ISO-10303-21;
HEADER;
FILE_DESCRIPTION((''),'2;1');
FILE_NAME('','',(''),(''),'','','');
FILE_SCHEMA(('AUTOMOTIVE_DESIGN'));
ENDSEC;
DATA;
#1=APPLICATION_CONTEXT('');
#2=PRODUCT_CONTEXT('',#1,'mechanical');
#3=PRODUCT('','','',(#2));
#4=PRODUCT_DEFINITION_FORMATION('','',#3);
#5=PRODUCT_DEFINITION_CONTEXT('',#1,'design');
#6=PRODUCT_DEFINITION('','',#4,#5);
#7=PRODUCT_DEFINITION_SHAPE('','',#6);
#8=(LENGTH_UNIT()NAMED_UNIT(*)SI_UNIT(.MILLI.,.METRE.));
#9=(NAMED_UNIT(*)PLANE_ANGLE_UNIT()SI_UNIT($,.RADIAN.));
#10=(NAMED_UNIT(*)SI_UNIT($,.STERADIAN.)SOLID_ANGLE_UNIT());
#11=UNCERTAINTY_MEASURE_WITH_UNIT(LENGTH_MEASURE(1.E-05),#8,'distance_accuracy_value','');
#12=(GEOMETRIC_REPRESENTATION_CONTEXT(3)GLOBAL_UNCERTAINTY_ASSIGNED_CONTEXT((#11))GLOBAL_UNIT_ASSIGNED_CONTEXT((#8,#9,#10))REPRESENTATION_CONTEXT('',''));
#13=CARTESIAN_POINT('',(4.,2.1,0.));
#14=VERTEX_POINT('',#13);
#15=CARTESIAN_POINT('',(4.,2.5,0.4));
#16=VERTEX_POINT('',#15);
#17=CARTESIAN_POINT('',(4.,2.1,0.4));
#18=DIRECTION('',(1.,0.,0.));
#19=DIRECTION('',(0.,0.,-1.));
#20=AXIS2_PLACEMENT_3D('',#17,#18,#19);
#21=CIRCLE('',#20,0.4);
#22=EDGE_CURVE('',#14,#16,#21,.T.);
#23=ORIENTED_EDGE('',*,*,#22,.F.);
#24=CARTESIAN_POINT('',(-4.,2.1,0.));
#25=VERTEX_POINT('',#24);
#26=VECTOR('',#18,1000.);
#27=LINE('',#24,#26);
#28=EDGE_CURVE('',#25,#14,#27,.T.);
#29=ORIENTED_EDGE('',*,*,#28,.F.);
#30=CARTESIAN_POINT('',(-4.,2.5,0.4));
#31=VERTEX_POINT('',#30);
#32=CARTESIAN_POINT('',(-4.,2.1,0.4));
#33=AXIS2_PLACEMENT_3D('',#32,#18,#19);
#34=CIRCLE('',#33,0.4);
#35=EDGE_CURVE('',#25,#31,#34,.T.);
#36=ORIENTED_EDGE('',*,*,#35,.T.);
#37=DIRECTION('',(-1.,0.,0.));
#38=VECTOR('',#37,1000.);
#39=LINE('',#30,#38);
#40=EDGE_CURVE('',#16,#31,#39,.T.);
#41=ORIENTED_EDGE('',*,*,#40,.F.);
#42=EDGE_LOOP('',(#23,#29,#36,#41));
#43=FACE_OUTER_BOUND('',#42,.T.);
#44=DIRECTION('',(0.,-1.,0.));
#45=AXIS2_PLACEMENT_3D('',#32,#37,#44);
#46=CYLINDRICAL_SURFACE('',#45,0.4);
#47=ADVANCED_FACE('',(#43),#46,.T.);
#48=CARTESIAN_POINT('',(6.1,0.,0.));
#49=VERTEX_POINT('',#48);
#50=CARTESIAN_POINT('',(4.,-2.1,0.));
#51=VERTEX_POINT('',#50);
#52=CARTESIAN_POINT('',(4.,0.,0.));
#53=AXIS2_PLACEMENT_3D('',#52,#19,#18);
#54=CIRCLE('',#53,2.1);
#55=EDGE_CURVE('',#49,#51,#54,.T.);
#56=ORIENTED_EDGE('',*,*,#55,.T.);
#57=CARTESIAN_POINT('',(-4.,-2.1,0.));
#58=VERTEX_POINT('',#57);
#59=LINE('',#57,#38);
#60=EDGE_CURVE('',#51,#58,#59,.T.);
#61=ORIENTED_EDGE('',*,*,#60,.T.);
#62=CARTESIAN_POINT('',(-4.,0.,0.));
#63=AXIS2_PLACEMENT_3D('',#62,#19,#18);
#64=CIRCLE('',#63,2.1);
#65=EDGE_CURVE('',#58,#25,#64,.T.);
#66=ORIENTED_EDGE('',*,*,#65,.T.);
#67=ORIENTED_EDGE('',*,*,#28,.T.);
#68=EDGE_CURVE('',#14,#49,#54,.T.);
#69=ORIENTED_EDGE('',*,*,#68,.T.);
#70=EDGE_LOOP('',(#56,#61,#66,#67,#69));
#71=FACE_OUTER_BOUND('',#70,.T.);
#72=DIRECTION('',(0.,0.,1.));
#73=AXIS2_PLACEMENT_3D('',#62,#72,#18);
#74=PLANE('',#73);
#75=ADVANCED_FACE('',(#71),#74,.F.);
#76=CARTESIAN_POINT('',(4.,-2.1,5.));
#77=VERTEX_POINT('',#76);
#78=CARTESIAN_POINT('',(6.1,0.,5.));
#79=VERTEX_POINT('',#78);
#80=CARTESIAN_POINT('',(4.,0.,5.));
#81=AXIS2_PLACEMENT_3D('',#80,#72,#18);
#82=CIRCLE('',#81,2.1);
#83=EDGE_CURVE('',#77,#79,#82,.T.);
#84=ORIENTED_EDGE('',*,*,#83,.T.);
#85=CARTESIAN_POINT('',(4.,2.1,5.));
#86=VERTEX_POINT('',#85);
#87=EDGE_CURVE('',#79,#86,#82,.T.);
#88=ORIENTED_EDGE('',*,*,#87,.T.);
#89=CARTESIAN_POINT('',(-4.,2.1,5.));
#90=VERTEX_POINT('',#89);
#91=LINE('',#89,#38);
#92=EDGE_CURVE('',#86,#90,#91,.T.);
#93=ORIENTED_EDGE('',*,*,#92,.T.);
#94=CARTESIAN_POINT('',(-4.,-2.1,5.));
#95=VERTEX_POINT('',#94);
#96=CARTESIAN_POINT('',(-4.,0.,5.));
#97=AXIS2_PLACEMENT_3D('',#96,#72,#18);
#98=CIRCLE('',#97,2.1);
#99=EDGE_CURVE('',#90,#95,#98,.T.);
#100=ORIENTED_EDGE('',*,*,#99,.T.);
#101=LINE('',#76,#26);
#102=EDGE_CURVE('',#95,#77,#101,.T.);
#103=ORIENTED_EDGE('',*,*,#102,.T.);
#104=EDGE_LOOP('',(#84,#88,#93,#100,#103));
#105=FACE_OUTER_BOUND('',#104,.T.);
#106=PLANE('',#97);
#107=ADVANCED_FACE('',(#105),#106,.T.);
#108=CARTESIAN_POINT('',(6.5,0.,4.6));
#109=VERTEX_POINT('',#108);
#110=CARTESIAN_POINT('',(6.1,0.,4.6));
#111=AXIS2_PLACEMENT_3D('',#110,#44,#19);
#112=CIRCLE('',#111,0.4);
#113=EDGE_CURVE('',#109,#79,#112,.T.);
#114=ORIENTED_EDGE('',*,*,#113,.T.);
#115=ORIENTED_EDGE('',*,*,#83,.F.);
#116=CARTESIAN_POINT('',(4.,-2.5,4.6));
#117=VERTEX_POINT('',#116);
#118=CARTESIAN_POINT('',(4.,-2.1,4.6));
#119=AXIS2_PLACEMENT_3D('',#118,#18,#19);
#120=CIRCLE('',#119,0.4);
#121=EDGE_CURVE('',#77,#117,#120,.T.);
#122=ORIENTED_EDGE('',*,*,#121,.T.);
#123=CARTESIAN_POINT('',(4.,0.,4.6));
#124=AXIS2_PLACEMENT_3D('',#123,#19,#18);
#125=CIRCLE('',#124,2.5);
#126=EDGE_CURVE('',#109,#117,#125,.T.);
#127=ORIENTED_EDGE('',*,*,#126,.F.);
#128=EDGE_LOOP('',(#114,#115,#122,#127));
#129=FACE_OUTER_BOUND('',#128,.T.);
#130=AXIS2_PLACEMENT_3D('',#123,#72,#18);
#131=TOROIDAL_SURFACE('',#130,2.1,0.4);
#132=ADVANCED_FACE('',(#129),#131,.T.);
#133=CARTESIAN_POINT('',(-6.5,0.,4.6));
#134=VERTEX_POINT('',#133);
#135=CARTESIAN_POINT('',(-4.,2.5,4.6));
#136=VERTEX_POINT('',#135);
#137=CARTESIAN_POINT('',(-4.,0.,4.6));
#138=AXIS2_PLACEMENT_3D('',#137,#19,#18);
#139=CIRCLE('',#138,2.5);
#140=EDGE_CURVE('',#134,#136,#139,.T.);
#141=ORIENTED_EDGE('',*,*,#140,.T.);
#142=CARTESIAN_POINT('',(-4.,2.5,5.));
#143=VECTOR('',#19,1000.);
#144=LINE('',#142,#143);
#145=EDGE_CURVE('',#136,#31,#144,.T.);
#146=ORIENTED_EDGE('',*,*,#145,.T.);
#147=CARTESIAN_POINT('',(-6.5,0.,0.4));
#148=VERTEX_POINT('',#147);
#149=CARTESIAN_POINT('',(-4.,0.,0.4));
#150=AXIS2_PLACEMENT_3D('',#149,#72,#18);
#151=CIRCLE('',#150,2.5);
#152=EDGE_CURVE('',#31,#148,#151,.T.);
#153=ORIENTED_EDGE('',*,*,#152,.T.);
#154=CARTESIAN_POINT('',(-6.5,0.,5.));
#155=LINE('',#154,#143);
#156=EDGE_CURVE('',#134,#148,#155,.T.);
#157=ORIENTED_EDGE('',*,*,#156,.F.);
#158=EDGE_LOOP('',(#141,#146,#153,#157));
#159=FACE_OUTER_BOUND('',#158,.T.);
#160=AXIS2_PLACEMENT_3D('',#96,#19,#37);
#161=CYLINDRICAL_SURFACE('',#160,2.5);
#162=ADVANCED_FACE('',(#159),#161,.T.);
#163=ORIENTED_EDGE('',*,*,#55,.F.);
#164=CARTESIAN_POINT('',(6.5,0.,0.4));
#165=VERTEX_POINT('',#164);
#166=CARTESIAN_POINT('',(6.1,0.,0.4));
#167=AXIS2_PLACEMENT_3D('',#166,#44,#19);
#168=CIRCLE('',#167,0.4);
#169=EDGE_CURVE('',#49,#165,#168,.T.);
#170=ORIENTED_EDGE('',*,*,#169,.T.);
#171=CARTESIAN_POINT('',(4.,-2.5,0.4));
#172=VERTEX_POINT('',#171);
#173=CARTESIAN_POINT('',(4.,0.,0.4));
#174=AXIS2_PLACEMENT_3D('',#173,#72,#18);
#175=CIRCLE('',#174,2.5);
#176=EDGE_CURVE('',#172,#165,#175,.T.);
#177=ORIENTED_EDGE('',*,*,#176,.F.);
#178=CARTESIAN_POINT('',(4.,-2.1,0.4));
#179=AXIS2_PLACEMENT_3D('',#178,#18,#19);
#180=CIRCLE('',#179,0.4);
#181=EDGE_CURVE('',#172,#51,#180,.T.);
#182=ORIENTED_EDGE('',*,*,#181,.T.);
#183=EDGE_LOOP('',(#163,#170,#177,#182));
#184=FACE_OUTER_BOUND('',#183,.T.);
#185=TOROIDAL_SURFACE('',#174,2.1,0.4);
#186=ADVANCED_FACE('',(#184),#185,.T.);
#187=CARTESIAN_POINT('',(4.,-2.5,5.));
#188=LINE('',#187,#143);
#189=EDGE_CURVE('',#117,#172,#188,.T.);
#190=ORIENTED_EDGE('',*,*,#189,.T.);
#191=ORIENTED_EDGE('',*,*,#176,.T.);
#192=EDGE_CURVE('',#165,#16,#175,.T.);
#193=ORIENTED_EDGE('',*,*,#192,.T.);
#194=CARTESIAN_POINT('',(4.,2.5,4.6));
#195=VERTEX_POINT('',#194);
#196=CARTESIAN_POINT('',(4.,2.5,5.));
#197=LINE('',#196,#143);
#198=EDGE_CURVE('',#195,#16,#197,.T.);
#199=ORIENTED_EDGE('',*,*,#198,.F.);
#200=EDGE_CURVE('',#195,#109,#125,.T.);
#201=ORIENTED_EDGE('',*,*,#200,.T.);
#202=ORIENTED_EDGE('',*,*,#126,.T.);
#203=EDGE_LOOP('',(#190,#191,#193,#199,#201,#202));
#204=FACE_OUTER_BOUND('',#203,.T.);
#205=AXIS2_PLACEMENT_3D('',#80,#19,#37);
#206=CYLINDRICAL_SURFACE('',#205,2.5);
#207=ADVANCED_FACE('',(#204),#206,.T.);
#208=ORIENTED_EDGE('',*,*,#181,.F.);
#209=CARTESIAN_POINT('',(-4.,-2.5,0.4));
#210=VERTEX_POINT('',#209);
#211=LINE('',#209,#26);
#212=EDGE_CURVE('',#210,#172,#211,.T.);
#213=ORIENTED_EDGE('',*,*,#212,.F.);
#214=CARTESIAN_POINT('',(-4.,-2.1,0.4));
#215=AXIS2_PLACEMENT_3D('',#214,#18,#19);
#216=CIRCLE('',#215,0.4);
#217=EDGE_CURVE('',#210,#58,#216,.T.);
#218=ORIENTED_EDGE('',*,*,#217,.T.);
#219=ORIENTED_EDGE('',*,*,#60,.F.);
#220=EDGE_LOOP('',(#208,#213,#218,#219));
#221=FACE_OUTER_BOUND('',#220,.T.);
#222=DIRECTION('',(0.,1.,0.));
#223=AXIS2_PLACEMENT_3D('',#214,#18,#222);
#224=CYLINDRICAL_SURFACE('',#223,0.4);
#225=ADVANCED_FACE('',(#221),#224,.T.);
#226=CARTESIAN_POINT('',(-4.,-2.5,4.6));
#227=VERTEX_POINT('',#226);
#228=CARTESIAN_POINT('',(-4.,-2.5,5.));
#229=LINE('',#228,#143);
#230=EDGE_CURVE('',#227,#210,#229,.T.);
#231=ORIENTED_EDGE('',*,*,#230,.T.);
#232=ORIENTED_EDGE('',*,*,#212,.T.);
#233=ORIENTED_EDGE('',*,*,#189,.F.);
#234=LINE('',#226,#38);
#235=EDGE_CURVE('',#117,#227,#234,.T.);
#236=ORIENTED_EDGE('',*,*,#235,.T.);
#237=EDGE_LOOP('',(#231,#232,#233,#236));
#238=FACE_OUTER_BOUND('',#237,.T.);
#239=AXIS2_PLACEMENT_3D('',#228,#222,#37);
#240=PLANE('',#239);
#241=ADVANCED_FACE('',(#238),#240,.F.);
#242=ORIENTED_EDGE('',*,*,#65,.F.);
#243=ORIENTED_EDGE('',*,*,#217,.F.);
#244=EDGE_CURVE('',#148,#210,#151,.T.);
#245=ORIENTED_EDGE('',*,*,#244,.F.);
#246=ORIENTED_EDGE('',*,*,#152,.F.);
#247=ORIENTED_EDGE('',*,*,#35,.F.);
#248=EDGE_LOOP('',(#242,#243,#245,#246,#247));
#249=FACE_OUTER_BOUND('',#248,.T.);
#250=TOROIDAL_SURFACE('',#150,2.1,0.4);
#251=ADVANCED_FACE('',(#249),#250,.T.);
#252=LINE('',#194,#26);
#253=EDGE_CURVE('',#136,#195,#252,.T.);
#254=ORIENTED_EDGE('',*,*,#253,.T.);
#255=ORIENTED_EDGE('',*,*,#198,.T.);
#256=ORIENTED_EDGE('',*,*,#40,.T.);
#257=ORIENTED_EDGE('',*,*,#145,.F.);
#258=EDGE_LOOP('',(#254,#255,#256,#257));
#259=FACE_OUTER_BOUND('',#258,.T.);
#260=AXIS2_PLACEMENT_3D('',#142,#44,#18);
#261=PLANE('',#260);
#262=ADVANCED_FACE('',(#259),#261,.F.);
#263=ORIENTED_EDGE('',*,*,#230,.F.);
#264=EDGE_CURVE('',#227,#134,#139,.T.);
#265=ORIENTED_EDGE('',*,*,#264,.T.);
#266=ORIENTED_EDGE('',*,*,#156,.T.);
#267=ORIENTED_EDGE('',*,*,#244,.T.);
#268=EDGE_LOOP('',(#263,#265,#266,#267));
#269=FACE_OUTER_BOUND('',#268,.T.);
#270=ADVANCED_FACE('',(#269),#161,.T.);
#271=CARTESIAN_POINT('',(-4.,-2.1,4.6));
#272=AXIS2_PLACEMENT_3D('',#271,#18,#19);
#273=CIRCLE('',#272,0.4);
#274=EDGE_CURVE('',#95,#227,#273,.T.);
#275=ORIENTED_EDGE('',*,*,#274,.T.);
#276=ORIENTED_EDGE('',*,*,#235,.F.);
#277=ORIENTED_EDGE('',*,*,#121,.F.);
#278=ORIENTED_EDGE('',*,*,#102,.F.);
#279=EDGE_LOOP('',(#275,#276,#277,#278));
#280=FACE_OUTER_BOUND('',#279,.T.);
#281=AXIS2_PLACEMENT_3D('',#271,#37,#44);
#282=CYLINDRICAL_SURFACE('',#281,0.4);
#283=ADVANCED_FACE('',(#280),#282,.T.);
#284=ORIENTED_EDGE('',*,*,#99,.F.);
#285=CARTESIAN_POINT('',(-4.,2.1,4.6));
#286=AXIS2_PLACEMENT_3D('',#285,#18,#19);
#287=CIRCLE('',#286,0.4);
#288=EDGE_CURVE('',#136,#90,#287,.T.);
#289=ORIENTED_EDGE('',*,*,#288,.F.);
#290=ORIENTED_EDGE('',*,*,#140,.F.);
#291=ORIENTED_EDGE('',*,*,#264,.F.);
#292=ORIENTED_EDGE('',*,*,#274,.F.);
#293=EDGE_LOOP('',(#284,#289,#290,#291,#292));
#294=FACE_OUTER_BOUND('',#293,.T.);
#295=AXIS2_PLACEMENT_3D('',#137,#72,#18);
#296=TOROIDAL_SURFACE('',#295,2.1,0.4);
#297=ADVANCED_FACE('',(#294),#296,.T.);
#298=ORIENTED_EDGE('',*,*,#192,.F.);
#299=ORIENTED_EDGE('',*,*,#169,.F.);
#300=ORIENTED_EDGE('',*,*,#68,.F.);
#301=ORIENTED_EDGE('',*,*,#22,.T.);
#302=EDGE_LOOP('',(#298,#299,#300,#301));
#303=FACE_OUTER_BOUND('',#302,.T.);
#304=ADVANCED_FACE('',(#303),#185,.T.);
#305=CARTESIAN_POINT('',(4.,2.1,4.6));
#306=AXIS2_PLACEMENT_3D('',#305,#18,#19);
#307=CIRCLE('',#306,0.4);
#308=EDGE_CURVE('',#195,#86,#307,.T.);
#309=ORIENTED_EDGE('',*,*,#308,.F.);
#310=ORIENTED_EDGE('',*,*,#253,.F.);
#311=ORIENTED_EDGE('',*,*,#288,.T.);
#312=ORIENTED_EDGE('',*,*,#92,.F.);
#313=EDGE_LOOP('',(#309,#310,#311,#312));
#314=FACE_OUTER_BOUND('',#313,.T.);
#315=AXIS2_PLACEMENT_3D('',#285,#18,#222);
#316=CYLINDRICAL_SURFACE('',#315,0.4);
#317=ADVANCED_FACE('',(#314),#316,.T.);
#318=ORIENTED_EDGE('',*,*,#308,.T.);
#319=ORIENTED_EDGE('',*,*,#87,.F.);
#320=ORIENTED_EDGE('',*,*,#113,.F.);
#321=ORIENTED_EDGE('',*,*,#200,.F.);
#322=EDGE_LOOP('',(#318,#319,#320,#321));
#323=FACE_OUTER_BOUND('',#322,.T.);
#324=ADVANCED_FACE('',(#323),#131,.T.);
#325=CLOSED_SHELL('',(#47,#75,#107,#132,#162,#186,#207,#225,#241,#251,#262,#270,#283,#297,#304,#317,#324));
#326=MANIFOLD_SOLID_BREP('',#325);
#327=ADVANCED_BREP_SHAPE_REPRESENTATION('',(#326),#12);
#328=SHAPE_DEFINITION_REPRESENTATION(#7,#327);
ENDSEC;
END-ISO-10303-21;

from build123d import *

# Parameters (mm, degrees)
BASE_EXTRUDE_DEPTH = 5
FILLET1_R          = 0.4


with BuildPart() as part:
    # Sketch1 → Base-Extrude (new body)
    with BuildSketch(Plane.XY):
        with BuildLine():
            Line((-4, 2.5), (4, 2.5))
            ThreePointArc((4, 2.5), (6.5, 0), (4, -2.5))
            Line((4, -2.5), (-4, -2.5))
            ThreePointArc((-4, -2.5), (-6.5, 0), (-4, 2.5))
        make_face()
    extrude(amount=BASE_EXTRUDE_DEPTH)

    # Fillet1
    fillet1_edges = [part.edges().sort_by_distance(p)[0] for p in [
        (6.5, 0, 5),
        (0, 2.5, 5),
        (-6.5, 0, 5),
        (0, 2.5, 0),
        (6.5, 0, 0),
        (0, -2.5, 0),
        (-6.5, 0, 0),
        (0, -2.5, 5),
    ]]
    fillet(fillet1_edges, radius=FILLET1_R)


solid = part.part
